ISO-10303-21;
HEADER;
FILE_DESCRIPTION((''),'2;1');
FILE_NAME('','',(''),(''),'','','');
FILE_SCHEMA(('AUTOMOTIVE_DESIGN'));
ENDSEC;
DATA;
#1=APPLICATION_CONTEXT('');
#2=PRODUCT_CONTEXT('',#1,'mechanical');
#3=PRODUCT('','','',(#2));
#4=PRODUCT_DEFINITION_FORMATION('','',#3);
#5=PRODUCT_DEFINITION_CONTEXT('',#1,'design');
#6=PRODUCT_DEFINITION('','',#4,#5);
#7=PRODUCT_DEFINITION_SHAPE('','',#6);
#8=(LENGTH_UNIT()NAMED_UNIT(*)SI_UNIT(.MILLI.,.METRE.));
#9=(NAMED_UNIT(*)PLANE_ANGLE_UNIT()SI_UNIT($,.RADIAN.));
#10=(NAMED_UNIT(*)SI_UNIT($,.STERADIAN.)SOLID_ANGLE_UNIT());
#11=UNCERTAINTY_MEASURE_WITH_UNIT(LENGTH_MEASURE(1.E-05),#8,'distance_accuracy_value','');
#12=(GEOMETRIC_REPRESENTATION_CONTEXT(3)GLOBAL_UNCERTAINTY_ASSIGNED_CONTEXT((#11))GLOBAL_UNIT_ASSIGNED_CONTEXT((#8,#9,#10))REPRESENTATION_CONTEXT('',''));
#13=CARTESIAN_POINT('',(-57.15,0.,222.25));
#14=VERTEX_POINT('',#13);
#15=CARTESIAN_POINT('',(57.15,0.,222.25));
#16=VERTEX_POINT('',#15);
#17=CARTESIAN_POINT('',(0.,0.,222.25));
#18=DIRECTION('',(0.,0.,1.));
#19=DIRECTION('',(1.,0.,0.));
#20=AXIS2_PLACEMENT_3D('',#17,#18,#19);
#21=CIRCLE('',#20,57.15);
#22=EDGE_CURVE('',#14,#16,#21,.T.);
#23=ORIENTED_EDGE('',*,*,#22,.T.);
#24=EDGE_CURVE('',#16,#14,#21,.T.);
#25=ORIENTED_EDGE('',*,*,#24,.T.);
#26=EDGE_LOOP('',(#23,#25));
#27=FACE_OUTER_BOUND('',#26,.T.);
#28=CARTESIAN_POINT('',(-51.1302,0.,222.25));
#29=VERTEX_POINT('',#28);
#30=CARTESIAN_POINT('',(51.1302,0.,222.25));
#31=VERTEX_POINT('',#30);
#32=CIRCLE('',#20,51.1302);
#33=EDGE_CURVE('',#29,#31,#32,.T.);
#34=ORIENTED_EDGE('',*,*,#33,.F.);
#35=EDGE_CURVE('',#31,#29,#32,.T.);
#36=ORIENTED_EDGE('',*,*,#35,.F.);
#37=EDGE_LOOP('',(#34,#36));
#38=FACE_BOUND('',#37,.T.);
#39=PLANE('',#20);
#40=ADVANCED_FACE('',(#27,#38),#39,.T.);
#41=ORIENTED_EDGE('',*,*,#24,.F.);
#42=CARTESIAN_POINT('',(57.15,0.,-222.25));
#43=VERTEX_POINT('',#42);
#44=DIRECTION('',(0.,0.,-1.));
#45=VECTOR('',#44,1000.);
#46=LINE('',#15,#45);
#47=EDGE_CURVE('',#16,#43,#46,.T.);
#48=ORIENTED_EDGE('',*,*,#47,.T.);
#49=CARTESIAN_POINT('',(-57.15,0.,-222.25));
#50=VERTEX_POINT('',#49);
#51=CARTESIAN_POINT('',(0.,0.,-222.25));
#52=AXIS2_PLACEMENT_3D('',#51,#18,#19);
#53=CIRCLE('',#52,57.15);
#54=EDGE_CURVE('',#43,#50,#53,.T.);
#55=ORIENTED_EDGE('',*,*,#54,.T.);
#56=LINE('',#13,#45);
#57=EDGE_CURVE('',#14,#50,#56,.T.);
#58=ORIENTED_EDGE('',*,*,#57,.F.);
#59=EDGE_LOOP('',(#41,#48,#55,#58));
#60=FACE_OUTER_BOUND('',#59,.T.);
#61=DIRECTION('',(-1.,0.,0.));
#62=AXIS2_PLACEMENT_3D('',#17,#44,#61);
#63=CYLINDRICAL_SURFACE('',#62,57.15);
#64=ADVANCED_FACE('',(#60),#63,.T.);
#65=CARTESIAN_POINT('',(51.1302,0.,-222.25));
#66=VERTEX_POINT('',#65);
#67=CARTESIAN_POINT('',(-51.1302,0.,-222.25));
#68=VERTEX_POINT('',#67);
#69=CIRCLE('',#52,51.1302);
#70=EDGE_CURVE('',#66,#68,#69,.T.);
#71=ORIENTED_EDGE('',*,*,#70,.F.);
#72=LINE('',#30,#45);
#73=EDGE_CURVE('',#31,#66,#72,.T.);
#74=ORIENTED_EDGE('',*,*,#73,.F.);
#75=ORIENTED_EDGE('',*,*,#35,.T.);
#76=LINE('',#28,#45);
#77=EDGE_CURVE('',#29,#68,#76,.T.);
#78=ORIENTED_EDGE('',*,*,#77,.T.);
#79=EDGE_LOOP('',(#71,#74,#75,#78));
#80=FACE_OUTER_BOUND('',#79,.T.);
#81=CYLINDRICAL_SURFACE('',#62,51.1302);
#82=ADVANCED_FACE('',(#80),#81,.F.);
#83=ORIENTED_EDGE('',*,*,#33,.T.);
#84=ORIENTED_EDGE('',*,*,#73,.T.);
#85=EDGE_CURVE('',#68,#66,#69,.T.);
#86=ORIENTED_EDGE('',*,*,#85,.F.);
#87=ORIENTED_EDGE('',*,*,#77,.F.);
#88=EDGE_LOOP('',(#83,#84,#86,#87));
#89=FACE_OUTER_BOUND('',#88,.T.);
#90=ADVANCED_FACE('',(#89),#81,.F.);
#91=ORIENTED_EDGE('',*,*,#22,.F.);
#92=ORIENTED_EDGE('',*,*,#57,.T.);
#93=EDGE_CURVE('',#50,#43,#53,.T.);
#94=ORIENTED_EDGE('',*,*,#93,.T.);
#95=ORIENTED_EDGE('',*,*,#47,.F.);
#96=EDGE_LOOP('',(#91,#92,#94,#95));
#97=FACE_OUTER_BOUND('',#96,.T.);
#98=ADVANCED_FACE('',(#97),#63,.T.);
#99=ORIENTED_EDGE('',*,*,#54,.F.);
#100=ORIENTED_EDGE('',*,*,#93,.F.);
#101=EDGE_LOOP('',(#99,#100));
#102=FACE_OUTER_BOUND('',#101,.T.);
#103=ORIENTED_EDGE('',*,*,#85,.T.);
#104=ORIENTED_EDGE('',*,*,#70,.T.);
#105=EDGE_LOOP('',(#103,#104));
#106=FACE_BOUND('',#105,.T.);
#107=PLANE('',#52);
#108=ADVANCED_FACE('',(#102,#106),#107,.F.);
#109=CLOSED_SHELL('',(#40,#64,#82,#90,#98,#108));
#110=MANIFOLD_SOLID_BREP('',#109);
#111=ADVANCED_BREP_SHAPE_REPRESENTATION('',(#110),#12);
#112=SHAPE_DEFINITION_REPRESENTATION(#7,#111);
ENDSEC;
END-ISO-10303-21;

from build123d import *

# Parameters (mm, degrees)
BOSS_EXTRUDE1_DEPTH      = 222.25
BOSS_EXTRUDE1_DEPTH_BACK = 222.25
SKETCH1_R                = 57.15
SKETCH1_R_2              = 51.1302


with BuildPart() as part:
    # Sketch1 → Boss-Extrude1 (new, two sides: drawn at the far end of the back side and taken through both)
    with BuildSketch(Plane.XY.offset(-BOSS_EXTRUDE1_DEPTH_BACK)):
        Circle(SKETCH1_R)
        Circle(SKETCH1_R_2, mode=Mode.SUBTRACT)
    extrude(amount=BOSS_EXTRUDE1_DEPTH + BOSS_EXTRUDE1_DEPTH_BACK)


solid = part.part
